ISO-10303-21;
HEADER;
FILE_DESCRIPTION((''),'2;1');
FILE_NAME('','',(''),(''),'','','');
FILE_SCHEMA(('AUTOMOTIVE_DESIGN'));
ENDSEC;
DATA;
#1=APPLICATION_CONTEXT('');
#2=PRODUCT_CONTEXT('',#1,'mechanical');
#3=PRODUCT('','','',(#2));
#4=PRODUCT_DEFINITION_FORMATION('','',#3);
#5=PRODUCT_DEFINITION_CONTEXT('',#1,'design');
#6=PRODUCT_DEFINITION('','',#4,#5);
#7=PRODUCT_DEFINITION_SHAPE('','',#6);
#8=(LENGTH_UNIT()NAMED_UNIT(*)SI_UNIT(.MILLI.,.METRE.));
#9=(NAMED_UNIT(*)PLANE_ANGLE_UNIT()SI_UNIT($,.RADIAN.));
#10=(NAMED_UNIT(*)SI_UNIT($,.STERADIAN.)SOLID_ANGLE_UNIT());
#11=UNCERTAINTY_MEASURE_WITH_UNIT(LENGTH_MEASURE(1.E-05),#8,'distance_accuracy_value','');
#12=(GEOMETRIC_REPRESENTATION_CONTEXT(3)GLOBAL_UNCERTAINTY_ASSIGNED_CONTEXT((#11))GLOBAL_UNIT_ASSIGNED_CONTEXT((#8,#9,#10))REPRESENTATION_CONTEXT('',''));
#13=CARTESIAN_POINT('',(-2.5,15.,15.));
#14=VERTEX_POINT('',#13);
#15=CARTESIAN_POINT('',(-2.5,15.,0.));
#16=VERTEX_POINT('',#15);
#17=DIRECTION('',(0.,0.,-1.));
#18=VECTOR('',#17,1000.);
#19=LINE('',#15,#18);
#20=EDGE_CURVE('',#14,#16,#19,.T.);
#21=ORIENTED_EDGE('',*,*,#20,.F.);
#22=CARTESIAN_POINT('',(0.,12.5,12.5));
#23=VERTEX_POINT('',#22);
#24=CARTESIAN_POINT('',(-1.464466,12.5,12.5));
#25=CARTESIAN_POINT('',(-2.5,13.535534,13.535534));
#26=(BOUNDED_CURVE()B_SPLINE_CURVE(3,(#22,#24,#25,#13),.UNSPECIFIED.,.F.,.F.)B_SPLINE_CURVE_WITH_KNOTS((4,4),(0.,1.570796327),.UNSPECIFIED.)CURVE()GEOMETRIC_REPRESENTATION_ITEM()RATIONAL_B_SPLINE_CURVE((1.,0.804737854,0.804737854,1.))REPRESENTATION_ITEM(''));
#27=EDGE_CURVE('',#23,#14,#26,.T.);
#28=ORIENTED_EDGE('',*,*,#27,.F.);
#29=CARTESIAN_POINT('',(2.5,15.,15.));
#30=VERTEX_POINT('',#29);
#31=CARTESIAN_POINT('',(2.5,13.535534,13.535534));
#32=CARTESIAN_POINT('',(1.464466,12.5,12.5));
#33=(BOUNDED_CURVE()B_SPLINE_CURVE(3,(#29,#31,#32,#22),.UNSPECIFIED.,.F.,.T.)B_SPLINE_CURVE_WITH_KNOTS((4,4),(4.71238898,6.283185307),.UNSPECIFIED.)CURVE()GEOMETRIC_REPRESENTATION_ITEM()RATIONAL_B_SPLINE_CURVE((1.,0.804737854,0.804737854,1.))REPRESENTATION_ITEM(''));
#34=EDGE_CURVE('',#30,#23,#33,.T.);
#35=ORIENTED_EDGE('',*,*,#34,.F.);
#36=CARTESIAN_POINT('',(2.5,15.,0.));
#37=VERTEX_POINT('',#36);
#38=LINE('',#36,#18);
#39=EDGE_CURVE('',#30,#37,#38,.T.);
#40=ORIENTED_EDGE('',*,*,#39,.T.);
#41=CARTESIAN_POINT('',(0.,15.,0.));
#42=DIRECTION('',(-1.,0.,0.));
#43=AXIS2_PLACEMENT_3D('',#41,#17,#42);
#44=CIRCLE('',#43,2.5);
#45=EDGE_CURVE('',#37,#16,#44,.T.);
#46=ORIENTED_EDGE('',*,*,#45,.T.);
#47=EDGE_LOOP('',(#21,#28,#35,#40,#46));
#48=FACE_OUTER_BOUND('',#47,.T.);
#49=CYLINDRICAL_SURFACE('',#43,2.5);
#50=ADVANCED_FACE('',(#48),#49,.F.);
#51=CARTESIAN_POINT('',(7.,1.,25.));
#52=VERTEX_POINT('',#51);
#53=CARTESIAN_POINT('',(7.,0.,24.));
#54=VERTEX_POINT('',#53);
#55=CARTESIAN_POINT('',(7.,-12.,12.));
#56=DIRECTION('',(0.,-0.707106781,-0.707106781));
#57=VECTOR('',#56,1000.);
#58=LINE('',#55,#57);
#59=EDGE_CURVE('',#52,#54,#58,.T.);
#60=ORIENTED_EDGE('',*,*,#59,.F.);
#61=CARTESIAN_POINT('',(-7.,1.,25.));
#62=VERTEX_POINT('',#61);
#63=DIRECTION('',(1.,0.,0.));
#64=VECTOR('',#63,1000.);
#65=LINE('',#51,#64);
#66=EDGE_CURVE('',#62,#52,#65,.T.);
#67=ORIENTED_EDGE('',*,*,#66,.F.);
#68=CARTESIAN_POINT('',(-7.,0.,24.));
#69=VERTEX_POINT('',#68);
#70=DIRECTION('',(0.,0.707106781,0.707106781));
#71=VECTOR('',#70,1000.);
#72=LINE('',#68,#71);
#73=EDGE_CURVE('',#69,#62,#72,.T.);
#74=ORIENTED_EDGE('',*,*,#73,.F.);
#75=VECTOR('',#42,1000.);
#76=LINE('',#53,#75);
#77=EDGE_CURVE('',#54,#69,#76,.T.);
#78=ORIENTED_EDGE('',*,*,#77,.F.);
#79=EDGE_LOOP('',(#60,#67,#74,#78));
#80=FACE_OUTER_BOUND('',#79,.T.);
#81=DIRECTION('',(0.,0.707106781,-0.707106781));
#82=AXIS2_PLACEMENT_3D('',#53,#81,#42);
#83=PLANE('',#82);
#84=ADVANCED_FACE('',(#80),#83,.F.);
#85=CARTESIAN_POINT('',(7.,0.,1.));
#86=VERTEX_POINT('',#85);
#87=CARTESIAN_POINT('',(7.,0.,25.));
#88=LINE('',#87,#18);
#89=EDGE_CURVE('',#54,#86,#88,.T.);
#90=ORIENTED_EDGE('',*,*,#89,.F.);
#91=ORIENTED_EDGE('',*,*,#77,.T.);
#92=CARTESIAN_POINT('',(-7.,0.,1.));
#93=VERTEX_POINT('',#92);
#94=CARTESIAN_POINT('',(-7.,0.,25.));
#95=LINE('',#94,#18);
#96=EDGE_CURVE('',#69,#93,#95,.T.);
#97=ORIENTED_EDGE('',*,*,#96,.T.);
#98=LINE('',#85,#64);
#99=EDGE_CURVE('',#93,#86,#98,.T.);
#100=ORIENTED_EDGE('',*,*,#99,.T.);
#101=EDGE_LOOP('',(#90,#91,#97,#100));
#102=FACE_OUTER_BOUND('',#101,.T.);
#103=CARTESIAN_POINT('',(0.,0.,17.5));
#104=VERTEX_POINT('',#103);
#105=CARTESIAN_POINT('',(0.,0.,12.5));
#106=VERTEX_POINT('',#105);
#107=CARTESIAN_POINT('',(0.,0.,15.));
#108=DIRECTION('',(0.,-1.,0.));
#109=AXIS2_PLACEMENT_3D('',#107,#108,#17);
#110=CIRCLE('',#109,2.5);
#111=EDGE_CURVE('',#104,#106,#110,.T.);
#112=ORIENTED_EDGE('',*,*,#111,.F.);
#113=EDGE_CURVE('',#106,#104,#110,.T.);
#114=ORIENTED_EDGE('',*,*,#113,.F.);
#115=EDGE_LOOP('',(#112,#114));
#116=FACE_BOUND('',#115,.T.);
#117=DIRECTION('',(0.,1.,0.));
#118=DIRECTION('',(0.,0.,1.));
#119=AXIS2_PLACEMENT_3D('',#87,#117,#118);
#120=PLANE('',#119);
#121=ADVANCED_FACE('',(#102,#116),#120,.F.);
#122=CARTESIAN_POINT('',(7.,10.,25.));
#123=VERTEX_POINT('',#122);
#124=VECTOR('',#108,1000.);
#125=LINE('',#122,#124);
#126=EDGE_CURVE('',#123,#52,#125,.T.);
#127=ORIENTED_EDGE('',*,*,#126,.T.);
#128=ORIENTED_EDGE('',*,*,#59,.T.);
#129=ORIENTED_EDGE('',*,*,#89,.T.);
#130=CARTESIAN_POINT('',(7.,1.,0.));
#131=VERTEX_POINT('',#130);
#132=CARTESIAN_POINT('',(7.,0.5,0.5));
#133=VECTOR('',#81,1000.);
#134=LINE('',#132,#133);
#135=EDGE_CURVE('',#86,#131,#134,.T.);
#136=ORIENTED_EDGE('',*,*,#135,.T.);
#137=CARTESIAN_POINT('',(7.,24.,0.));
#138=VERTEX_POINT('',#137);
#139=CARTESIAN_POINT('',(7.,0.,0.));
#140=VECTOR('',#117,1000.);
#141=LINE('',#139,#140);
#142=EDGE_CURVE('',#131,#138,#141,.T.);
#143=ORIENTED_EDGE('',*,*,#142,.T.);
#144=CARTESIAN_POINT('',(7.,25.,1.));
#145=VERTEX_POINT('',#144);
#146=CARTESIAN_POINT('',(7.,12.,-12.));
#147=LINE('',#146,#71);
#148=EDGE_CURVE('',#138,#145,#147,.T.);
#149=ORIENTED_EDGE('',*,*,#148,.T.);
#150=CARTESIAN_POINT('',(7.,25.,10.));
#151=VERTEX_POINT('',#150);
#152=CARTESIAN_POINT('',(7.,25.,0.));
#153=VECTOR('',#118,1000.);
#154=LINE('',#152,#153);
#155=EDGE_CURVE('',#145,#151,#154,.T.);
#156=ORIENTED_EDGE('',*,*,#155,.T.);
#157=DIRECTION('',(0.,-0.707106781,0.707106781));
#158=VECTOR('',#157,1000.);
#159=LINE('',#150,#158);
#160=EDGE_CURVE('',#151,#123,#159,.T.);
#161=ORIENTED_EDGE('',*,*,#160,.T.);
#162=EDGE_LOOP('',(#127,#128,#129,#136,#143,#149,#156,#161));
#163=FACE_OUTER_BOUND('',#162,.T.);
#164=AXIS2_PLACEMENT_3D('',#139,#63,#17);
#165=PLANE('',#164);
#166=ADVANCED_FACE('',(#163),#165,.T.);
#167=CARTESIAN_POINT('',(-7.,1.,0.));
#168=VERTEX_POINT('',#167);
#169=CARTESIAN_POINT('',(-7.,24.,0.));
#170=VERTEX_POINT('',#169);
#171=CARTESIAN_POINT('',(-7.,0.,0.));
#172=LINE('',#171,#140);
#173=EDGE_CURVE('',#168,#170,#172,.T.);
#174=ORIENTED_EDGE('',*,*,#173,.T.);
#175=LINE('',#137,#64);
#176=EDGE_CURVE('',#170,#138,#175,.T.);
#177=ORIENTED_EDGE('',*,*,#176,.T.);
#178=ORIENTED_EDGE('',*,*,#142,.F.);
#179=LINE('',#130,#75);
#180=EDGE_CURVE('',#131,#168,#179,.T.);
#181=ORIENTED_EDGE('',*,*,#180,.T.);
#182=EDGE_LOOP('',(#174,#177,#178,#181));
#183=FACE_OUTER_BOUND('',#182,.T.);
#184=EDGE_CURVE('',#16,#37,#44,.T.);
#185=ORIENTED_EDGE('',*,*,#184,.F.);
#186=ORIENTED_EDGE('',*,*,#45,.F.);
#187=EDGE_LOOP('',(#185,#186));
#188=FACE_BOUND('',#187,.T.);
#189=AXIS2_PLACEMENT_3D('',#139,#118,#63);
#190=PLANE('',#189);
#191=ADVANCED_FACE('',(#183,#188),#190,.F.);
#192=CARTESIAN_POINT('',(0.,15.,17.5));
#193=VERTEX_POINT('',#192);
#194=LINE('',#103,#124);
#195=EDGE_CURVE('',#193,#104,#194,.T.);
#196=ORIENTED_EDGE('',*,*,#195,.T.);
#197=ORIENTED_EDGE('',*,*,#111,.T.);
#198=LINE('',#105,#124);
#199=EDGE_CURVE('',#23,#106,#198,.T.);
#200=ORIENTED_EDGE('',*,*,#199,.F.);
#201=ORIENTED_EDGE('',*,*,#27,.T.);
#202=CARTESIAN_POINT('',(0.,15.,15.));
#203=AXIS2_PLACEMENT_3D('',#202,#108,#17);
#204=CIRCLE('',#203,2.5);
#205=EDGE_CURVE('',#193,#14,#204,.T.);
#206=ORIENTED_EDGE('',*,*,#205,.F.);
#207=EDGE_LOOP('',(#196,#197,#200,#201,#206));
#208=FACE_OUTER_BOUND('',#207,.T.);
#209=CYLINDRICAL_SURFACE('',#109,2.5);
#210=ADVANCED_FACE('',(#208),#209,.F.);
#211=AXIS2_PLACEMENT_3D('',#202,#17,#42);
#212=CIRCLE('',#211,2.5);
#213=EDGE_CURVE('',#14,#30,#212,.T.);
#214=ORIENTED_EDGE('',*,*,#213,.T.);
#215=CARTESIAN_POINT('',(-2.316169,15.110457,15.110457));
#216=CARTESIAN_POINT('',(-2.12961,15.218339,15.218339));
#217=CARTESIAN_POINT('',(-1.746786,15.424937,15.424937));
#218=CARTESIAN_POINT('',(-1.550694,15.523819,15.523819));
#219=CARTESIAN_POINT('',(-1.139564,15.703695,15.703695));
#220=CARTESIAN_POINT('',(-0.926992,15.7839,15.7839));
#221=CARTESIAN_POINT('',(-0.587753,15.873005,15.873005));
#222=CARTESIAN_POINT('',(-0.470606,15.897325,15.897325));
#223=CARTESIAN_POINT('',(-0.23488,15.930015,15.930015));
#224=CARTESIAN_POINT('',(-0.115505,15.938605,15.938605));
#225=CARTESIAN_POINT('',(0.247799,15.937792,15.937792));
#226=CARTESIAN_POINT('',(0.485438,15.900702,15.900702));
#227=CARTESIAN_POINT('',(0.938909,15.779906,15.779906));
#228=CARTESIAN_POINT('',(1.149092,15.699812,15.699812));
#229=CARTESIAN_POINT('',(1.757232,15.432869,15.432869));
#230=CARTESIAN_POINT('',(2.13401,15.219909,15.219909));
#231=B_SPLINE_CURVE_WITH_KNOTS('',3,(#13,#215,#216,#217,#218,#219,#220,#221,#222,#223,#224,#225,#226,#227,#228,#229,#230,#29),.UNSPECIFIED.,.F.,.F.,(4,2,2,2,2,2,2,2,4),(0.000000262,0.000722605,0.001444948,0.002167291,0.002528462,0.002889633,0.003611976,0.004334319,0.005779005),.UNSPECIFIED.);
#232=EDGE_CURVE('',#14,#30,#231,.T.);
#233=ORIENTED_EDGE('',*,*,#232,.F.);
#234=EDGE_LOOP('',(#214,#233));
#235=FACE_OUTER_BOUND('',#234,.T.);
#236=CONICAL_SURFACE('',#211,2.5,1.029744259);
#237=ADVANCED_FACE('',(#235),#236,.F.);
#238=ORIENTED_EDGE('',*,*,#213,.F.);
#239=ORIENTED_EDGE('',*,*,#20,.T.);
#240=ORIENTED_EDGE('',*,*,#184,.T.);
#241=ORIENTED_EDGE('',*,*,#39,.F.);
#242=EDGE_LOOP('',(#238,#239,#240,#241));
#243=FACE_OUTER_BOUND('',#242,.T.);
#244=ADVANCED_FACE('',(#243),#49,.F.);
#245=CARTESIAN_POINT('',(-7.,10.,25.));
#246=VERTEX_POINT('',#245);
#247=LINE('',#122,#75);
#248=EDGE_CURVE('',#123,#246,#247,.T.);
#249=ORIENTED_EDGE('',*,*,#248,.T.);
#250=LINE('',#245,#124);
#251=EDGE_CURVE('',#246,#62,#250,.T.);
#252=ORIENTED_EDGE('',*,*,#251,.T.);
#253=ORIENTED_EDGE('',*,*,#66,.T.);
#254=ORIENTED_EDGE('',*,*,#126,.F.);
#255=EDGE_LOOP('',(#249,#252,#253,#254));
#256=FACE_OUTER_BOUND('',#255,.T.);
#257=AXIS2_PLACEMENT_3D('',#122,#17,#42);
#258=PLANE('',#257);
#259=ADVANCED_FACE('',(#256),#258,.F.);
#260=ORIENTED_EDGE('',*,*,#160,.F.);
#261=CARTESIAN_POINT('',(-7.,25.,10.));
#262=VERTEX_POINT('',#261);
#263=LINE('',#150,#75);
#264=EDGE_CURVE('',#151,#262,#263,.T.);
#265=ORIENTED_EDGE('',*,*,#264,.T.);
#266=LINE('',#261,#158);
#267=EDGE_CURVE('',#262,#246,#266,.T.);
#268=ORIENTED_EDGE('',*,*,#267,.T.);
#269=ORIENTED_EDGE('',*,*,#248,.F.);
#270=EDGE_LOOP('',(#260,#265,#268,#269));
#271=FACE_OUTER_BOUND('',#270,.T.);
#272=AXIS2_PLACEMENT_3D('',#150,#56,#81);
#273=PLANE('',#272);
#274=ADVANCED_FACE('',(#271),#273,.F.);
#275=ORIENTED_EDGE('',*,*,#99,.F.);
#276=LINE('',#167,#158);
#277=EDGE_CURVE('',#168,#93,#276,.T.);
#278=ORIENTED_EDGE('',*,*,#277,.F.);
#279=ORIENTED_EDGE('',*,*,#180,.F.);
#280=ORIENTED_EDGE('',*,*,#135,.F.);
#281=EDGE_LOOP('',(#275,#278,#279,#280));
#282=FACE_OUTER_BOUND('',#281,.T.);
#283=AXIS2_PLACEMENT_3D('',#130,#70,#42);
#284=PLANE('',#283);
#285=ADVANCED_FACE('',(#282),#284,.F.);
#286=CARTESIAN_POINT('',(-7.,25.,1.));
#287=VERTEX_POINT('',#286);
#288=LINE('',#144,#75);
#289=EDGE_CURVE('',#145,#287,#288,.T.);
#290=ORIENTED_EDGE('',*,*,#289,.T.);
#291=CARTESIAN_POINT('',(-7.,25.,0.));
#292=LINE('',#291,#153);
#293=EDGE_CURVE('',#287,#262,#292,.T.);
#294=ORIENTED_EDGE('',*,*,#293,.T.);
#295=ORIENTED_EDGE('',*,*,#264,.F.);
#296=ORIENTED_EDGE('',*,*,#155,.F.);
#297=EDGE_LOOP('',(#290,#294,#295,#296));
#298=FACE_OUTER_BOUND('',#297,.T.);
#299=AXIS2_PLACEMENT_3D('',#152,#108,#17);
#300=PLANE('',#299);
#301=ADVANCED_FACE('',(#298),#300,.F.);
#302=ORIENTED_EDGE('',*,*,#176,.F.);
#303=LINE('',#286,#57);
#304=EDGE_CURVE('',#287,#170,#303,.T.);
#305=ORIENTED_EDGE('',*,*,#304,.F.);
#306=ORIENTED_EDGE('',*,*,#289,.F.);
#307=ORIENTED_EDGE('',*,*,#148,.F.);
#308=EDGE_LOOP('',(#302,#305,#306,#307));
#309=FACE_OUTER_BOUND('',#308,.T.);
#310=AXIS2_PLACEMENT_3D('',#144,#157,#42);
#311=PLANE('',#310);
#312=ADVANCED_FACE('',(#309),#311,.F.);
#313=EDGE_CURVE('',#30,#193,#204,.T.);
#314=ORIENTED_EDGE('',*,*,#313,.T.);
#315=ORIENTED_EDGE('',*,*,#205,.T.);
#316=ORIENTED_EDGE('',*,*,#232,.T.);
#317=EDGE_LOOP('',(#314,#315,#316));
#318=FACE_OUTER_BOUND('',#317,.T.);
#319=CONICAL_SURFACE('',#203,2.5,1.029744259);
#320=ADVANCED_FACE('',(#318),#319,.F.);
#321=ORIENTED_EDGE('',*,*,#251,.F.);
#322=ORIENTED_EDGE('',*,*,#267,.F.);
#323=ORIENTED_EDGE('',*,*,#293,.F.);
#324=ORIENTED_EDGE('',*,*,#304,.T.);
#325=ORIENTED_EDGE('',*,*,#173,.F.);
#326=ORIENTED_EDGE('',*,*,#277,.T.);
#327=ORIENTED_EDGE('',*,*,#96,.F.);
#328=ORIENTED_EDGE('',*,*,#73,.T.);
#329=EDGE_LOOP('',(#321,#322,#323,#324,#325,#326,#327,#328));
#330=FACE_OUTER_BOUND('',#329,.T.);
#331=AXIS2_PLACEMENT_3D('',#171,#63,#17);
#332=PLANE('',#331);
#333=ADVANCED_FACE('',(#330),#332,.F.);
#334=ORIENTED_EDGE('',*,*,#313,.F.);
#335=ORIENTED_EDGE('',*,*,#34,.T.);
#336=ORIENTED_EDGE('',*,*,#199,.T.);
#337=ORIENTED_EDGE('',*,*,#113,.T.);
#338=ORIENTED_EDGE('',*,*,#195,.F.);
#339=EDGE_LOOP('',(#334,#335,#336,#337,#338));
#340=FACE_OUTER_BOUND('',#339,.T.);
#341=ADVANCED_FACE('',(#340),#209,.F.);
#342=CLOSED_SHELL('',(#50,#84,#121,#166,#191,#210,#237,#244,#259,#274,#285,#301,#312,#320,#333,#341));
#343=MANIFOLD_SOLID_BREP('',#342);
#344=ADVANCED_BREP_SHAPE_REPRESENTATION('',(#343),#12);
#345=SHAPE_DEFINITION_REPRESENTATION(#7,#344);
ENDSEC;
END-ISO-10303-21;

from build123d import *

# Parameters (mm, degrees)
BOSS_EXTRUDE1_DEPTH   = 7
M6_TAPPED_HOLE1_D     = 5
M6_TAPPED_HOLE1_DEPTH = 15
M6_TAPPED_HOLE1_TIP   = 1.502151548
M6_TAPPED_HOLE2_D     = 5
M6_TAPPED_HOLE2_DEPTH = 15
M6_TAPPED_HOLE2_TIP   = 1.502151548
CHAMFER1_SIZE         = 1


with BuildPart() as part:
    # Sketch1 → Boss-Extrude1 (new, symmetric)
    with BuildSketch(Plane(origin=(0, 0, 0), x_dir=(0, 0, -1), z_dir=(1, 0, 0))):
        Polygon((0, 0), (0, 25), (-10, 25), (-25, 10), (-25, 0), align=None)
    extrude(amount=BOSS_EXTRUDE1_DEPTH, both=True)

    # M6 Tapped Hole1
    with Locations(Plane(origin=(0, 0, 0), x_dir=(-1, 0, 0), z_dir=(0, -1, 0))):
        with Locations((0, -15)):
            Hole(M6_TAPPED_HOLE1_D / 2, depth=M6_TAPPED_HOLE1_DEPTH)
            with Locations((0, 0, -(M6_TAPPED_HOLE1_DEPTH + M6_TAPPED_HOLE1_TIP / 2))):  # 118° drill point
                Cone(0, M6_TAPPED_HOLE1_D / 2, M6_TAPPED_HOLE1_TIP, mode=Mode.SUBTRACT)

    # M6 Tapped Hole2
    with Locations(Plane(origin=(0, 0, 0), x_dir=(-1, 0, 0), z_dir=(0, 0, -1))):
        with Locations((0, 15)):
            Hole(M6_TAPPED_HOLE2_D / 2, depth=M6_TAPPED_HOLE2_DEPTH)
            with Locations((0, 0, -(M6_TAPPED_HOLE2_DEPTH + M6_TAPPED_HOLE2_TIP / 2))):  # 118° drill point
                Cone(0, M6_TAPPED_HOLE2_D / 2, M6_TAPPED_HOLE2_TIP, mode=Mode.SUBTRACT)

    # Chamfer1
    chamfer1_edges = [part.edges().sort_by_distance(p)[0] for p in [
        (0, 0, 25),
        (0, 25, 0),
        (0, 0, 0),
    ]]
    chamfer(chamfer1_edges, length=CHAMFER1_SIZE)


solid = part.part
